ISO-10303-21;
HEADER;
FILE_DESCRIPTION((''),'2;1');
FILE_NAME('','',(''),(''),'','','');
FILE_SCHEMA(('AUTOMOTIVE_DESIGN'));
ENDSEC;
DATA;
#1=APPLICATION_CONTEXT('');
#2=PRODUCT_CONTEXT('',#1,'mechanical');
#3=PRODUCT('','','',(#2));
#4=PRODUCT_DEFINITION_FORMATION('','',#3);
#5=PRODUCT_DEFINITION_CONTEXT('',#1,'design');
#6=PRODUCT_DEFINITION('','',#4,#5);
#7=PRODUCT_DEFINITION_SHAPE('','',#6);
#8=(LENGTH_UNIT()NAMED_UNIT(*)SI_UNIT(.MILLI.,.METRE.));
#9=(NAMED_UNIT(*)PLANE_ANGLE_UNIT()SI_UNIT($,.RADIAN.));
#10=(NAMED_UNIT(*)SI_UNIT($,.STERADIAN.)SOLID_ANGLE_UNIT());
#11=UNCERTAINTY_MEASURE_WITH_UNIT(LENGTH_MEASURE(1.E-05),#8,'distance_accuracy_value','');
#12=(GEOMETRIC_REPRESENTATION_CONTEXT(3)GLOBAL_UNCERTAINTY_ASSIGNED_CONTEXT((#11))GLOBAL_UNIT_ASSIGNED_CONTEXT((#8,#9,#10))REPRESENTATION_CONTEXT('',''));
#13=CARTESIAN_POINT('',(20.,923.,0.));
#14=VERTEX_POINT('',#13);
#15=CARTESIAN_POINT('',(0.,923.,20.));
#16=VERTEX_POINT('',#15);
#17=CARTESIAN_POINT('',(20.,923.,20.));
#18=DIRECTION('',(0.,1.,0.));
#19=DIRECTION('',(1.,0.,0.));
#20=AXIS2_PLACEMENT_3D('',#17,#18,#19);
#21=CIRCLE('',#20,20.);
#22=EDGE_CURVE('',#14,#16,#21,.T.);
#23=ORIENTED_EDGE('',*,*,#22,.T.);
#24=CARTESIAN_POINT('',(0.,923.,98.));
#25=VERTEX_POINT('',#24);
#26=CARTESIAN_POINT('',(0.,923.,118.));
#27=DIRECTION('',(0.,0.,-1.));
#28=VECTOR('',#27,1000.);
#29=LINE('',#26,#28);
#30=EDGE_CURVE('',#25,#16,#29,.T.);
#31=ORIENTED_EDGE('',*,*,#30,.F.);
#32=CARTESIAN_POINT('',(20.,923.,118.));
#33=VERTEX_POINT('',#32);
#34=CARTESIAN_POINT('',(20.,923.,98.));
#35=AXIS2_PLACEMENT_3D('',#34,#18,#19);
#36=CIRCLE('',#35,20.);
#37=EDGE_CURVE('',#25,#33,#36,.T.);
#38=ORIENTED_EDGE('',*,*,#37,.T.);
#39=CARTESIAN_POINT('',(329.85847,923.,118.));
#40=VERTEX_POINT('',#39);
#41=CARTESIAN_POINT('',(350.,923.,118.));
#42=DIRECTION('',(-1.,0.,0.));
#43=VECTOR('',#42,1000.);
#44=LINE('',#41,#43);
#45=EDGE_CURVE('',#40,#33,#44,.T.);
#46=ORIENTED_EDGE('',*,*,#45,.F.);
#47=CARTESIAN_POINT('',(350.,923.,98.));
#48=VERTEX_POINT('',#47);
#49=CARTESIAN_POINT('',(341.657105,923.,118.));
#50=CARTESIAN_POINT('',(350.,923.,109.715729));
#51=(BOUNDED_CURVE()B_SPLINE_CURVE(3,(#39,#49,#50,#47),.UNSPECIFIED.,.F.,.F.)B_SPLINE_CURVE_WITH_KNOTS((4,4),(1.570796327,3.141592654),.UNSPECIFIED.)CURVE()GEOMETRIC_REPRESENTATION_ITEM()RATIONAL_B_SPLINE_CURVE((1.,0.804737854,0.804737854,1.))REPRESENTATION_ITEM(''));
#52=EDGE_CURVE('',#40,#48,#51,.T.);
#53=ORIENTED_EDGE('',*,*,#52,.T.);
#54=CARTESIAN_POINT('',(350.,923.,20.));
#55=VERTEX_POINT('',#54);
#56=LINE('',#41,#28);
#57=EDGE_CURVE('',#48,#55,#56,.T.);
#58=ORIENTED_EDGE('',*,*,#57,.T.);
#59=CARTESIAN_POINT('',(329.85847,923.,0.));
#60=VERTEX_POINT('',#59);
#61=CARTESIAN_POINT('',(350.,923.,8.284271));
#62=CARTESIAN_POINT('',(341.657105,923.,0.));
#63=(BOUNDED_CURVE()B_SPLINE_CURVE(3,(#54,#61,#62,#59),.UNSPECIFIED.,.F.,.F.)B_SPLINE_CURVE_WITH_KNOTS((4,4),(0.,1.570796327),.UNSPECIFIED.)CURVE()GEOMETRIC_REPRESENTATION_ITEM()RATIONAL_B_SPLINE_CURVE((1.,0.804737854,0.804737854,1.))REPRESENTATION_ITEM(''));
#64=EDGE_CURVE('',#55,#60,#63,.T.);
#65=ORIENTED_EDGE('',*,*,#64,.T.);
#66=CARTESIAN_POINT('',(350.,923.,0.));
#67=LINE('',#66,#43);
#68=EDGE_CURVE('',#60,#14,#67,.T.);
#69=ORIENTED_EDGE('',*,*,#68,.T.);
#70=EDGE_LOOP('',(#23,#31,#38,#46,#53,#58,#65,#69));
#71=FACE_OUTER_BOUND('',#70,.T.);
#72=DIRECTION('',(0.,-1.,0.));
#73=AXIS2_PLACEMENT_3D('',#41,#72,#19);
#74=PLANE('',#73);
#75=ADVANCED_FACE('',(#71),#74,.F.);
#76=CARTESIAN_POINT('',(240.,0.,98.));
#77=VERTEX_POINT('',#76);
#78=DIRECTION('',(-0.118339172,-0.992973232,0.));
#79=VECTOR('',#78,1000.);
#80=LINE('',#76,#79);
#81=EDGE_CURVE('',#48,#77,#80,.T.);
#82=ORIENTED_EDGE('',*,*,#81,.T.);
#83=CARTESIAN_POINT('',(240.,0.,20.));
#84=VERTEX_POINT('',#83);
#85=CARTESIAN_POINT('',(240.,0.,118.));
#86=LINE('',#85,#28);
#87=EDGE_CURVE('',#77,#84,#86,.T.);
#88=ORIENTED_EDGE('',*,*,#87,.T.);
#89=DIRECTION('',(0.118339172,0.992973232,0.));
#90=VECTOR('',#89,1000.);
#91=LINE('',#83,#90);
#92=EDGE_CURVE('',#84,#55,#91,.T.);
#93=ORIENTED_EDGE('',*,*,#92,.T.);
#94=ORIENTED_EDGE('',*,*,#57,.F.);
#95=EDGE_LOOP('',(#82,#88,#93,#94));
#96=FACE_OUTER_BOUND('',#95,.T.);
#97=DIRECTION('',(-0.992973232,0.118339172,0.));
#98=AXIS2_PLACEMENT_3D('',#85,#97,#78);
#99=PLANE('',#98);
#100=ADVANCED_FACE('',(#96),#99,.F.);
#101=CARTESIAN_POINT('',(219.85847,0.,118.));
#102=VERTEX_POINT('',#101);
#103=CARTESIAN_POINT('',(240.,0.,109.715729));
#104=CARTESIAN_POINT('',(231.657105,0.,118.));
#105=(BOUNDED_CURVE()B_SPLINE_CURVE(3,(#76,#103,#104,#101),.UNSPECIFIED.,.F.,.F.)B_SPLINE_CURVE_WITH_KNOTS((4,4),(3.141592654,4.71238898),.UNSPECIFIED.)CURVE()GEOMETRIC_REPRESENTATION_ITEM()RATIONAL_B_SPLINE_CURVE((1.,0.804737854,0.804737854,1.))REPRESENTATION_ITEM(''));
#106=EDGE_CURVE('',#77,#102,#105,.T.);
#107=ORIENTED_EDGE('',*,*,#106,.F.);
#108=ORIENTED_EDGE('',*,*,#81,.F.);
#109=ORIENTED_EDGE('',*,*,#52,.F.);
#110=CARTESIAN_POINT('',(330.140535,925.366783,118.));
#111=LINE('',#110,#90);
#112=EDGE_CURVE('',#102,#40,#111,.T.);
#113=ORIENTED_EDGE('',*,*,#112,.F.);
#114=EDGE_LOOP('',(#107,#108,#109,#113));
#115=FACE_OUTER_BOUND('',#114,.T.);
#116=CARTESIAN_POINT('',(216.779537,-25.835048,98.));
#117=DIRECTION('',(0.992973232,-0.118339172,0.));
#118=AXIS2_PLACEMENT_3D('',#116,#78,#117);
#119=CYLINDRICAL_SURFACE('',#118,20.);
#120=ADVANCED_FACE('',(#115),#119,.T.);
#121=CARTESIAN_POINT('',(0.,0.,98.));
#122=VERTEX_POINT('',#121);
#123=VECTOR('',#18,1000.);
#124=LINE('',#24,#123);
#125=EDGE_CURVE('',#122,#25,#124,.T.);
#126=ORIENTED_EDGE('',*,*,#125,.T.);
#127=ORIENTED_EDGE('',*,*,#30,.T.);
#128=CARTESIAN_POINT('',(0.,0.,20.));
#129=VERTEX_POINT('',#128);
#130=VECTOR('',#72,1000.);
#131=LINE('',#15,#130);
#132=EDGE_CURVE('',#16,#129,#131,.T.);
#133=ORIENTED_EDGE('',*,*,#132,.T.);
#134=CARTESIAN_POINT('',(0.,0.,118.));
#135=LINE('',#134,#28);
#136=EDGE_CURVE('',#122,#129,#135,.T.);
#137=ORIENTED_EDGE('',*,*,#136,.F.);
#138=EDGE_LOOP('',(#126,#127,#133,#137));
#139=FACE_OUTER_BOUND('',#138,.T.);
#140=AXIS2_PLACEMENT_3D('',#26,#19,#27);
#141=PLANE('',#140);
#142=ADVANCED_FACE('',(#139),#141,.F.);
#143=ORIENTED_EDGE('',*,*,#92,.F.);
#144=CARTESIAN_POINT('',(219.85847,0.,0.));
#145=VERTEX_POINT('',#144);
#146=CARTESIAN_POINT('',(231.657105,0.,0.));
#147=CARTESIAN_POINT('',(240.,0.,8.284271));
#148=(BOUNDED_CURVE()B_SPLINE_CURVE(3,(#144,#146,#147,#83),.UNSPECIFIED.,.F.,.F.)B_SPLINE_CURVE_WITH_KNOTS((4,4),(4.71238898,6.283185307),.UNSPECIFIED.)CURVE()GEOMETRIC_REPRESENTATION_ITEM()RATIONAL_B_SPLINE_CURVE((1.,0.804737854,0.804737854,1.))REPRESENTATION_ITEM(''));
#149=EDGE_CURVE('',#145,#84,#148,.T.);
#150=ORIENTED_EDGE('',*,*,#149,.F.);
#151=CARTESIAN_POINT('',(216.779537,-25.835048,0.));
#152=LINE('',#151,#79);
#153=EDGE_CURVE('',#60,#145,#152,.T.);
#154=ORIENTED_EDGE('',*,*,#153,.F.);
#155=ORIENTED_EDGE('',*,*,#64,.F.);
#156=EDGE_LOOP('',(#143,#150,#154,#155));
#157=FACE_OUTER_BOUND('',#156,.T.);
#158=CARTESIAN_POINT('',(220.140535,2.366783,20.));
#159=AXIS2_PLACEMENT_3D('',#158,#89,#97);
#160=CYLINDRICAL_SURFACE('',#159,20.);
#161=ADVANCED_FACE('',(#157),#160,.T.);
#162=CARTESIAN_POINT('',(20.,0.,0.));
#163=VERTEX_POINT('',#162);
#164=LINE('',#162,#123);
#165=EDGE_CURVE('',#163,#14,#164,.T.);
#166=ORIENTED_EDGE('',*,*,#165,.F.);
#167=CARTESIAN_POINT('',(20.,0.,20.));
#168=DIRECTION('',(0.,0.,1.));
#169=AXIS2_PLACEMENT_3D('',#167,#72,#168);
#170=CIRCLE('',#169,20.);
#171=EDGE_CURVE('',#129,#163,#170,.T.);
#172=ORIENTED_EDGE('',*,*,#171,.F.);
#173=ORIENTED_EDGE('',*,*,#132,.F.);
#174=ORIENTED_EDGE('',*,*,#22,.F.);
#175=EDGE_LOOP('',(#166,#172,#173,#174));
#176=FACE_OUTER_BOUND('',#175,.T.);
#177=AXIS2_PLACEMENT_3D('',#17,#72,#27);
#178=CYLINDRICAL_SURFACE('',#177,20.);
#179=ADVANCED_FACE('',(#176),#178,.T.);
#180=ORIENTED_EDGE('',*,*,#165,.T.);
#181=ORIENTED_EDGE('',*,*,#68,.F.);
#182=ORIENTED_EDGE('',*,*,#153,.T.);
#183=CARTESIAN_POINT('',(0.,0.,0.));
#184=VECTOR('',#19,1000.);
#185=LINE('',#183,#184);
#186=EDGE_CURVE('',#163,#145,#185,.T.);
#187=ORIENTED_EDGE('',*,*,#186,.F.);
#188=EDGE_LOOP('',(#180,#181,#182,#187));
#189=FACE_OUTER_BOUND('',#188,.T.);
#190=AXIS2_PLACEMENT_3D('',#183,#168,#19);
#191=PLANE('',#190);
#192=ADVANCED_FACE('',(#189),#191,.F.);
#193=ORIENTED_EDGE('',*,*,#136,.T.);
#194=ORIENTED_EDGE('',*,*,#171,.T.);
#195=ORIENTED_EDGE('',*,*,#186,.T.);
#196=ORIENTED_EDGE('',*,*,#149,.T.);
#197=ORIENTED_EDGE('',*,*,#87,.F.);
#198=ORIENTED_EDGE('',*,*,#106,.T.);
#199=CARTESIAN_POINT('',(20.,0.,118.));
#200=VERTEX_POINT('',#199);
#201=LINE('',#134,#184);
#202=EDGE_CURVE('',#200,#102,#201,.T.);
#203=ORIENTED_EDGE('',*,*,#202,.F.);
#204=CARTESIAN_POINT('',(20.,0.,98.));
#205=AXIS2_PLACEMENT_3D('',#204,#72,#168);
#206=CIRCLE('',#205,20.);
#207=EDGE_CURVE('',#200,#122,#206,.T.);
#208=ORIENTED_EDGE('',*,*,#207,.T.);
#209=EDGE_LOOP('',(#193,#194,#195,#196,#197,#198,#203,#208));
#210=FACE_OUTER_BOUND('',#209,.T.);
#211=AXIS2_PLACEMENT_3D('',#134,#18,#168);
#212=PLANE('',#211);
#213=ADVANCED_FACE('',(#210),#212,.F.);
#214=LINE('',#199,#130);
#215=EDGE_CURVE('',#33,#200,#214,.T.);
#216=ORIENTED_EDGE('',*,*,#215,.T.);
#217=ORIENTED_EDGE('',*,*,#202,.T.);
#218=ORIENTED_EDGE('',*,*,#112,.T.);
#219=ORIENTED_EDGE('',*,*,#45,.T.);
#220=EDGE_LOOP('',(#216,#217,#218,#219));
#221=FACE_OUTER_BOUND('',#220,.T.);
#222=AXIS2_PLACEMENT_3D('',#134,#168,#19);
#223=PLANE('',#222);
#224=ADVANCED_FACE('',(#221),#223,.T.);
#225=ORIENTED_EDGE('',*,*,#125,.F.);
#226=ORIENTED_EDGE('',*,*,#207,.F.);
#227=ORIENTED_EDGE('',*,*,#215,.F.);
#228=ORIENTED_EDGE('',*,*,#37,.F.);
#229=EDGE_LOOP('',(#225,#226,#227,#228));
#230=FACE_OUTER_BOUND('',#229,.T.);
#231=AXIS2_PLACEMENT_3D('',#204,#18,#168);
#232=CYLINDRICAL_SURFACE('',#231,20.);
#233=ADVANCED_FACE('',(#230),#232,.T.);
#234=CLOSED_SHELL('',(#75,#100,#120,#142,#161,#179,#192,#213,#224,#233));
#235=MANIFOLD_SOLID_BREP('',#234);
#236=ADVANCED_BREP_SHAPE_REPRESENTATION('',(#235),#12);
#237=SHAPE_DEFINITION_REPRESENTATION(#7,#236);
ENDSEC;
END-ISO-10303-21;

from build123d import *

# Parameters (mm, degrees)
BOSS_EXTRUDE1_DEPTH = 118
FILLET1_R           = 20


with BuildPart() as part:
    # Sketch1 → Boss-Extrude1 (new body)
    with BuildSketch(Plane.XY):
        Polygon((0, 0), (240, 0), (350, 923), (0, 923), align=None)
    extrude(amount=BOSS_EXTRUDE1_DEPTH)

    # Fillet1
    fillet1_edges = [part.edges().sort_by_distance(p)[0] for p in [
        (295, 461.5, 118),
        (0, 461.5, 118),
        (295, 461.5, 0),
        (0, 461.5, 0),
    ]]
    fillet(fillet1_edges, radius=FILLET1_R)


solid = part.part
